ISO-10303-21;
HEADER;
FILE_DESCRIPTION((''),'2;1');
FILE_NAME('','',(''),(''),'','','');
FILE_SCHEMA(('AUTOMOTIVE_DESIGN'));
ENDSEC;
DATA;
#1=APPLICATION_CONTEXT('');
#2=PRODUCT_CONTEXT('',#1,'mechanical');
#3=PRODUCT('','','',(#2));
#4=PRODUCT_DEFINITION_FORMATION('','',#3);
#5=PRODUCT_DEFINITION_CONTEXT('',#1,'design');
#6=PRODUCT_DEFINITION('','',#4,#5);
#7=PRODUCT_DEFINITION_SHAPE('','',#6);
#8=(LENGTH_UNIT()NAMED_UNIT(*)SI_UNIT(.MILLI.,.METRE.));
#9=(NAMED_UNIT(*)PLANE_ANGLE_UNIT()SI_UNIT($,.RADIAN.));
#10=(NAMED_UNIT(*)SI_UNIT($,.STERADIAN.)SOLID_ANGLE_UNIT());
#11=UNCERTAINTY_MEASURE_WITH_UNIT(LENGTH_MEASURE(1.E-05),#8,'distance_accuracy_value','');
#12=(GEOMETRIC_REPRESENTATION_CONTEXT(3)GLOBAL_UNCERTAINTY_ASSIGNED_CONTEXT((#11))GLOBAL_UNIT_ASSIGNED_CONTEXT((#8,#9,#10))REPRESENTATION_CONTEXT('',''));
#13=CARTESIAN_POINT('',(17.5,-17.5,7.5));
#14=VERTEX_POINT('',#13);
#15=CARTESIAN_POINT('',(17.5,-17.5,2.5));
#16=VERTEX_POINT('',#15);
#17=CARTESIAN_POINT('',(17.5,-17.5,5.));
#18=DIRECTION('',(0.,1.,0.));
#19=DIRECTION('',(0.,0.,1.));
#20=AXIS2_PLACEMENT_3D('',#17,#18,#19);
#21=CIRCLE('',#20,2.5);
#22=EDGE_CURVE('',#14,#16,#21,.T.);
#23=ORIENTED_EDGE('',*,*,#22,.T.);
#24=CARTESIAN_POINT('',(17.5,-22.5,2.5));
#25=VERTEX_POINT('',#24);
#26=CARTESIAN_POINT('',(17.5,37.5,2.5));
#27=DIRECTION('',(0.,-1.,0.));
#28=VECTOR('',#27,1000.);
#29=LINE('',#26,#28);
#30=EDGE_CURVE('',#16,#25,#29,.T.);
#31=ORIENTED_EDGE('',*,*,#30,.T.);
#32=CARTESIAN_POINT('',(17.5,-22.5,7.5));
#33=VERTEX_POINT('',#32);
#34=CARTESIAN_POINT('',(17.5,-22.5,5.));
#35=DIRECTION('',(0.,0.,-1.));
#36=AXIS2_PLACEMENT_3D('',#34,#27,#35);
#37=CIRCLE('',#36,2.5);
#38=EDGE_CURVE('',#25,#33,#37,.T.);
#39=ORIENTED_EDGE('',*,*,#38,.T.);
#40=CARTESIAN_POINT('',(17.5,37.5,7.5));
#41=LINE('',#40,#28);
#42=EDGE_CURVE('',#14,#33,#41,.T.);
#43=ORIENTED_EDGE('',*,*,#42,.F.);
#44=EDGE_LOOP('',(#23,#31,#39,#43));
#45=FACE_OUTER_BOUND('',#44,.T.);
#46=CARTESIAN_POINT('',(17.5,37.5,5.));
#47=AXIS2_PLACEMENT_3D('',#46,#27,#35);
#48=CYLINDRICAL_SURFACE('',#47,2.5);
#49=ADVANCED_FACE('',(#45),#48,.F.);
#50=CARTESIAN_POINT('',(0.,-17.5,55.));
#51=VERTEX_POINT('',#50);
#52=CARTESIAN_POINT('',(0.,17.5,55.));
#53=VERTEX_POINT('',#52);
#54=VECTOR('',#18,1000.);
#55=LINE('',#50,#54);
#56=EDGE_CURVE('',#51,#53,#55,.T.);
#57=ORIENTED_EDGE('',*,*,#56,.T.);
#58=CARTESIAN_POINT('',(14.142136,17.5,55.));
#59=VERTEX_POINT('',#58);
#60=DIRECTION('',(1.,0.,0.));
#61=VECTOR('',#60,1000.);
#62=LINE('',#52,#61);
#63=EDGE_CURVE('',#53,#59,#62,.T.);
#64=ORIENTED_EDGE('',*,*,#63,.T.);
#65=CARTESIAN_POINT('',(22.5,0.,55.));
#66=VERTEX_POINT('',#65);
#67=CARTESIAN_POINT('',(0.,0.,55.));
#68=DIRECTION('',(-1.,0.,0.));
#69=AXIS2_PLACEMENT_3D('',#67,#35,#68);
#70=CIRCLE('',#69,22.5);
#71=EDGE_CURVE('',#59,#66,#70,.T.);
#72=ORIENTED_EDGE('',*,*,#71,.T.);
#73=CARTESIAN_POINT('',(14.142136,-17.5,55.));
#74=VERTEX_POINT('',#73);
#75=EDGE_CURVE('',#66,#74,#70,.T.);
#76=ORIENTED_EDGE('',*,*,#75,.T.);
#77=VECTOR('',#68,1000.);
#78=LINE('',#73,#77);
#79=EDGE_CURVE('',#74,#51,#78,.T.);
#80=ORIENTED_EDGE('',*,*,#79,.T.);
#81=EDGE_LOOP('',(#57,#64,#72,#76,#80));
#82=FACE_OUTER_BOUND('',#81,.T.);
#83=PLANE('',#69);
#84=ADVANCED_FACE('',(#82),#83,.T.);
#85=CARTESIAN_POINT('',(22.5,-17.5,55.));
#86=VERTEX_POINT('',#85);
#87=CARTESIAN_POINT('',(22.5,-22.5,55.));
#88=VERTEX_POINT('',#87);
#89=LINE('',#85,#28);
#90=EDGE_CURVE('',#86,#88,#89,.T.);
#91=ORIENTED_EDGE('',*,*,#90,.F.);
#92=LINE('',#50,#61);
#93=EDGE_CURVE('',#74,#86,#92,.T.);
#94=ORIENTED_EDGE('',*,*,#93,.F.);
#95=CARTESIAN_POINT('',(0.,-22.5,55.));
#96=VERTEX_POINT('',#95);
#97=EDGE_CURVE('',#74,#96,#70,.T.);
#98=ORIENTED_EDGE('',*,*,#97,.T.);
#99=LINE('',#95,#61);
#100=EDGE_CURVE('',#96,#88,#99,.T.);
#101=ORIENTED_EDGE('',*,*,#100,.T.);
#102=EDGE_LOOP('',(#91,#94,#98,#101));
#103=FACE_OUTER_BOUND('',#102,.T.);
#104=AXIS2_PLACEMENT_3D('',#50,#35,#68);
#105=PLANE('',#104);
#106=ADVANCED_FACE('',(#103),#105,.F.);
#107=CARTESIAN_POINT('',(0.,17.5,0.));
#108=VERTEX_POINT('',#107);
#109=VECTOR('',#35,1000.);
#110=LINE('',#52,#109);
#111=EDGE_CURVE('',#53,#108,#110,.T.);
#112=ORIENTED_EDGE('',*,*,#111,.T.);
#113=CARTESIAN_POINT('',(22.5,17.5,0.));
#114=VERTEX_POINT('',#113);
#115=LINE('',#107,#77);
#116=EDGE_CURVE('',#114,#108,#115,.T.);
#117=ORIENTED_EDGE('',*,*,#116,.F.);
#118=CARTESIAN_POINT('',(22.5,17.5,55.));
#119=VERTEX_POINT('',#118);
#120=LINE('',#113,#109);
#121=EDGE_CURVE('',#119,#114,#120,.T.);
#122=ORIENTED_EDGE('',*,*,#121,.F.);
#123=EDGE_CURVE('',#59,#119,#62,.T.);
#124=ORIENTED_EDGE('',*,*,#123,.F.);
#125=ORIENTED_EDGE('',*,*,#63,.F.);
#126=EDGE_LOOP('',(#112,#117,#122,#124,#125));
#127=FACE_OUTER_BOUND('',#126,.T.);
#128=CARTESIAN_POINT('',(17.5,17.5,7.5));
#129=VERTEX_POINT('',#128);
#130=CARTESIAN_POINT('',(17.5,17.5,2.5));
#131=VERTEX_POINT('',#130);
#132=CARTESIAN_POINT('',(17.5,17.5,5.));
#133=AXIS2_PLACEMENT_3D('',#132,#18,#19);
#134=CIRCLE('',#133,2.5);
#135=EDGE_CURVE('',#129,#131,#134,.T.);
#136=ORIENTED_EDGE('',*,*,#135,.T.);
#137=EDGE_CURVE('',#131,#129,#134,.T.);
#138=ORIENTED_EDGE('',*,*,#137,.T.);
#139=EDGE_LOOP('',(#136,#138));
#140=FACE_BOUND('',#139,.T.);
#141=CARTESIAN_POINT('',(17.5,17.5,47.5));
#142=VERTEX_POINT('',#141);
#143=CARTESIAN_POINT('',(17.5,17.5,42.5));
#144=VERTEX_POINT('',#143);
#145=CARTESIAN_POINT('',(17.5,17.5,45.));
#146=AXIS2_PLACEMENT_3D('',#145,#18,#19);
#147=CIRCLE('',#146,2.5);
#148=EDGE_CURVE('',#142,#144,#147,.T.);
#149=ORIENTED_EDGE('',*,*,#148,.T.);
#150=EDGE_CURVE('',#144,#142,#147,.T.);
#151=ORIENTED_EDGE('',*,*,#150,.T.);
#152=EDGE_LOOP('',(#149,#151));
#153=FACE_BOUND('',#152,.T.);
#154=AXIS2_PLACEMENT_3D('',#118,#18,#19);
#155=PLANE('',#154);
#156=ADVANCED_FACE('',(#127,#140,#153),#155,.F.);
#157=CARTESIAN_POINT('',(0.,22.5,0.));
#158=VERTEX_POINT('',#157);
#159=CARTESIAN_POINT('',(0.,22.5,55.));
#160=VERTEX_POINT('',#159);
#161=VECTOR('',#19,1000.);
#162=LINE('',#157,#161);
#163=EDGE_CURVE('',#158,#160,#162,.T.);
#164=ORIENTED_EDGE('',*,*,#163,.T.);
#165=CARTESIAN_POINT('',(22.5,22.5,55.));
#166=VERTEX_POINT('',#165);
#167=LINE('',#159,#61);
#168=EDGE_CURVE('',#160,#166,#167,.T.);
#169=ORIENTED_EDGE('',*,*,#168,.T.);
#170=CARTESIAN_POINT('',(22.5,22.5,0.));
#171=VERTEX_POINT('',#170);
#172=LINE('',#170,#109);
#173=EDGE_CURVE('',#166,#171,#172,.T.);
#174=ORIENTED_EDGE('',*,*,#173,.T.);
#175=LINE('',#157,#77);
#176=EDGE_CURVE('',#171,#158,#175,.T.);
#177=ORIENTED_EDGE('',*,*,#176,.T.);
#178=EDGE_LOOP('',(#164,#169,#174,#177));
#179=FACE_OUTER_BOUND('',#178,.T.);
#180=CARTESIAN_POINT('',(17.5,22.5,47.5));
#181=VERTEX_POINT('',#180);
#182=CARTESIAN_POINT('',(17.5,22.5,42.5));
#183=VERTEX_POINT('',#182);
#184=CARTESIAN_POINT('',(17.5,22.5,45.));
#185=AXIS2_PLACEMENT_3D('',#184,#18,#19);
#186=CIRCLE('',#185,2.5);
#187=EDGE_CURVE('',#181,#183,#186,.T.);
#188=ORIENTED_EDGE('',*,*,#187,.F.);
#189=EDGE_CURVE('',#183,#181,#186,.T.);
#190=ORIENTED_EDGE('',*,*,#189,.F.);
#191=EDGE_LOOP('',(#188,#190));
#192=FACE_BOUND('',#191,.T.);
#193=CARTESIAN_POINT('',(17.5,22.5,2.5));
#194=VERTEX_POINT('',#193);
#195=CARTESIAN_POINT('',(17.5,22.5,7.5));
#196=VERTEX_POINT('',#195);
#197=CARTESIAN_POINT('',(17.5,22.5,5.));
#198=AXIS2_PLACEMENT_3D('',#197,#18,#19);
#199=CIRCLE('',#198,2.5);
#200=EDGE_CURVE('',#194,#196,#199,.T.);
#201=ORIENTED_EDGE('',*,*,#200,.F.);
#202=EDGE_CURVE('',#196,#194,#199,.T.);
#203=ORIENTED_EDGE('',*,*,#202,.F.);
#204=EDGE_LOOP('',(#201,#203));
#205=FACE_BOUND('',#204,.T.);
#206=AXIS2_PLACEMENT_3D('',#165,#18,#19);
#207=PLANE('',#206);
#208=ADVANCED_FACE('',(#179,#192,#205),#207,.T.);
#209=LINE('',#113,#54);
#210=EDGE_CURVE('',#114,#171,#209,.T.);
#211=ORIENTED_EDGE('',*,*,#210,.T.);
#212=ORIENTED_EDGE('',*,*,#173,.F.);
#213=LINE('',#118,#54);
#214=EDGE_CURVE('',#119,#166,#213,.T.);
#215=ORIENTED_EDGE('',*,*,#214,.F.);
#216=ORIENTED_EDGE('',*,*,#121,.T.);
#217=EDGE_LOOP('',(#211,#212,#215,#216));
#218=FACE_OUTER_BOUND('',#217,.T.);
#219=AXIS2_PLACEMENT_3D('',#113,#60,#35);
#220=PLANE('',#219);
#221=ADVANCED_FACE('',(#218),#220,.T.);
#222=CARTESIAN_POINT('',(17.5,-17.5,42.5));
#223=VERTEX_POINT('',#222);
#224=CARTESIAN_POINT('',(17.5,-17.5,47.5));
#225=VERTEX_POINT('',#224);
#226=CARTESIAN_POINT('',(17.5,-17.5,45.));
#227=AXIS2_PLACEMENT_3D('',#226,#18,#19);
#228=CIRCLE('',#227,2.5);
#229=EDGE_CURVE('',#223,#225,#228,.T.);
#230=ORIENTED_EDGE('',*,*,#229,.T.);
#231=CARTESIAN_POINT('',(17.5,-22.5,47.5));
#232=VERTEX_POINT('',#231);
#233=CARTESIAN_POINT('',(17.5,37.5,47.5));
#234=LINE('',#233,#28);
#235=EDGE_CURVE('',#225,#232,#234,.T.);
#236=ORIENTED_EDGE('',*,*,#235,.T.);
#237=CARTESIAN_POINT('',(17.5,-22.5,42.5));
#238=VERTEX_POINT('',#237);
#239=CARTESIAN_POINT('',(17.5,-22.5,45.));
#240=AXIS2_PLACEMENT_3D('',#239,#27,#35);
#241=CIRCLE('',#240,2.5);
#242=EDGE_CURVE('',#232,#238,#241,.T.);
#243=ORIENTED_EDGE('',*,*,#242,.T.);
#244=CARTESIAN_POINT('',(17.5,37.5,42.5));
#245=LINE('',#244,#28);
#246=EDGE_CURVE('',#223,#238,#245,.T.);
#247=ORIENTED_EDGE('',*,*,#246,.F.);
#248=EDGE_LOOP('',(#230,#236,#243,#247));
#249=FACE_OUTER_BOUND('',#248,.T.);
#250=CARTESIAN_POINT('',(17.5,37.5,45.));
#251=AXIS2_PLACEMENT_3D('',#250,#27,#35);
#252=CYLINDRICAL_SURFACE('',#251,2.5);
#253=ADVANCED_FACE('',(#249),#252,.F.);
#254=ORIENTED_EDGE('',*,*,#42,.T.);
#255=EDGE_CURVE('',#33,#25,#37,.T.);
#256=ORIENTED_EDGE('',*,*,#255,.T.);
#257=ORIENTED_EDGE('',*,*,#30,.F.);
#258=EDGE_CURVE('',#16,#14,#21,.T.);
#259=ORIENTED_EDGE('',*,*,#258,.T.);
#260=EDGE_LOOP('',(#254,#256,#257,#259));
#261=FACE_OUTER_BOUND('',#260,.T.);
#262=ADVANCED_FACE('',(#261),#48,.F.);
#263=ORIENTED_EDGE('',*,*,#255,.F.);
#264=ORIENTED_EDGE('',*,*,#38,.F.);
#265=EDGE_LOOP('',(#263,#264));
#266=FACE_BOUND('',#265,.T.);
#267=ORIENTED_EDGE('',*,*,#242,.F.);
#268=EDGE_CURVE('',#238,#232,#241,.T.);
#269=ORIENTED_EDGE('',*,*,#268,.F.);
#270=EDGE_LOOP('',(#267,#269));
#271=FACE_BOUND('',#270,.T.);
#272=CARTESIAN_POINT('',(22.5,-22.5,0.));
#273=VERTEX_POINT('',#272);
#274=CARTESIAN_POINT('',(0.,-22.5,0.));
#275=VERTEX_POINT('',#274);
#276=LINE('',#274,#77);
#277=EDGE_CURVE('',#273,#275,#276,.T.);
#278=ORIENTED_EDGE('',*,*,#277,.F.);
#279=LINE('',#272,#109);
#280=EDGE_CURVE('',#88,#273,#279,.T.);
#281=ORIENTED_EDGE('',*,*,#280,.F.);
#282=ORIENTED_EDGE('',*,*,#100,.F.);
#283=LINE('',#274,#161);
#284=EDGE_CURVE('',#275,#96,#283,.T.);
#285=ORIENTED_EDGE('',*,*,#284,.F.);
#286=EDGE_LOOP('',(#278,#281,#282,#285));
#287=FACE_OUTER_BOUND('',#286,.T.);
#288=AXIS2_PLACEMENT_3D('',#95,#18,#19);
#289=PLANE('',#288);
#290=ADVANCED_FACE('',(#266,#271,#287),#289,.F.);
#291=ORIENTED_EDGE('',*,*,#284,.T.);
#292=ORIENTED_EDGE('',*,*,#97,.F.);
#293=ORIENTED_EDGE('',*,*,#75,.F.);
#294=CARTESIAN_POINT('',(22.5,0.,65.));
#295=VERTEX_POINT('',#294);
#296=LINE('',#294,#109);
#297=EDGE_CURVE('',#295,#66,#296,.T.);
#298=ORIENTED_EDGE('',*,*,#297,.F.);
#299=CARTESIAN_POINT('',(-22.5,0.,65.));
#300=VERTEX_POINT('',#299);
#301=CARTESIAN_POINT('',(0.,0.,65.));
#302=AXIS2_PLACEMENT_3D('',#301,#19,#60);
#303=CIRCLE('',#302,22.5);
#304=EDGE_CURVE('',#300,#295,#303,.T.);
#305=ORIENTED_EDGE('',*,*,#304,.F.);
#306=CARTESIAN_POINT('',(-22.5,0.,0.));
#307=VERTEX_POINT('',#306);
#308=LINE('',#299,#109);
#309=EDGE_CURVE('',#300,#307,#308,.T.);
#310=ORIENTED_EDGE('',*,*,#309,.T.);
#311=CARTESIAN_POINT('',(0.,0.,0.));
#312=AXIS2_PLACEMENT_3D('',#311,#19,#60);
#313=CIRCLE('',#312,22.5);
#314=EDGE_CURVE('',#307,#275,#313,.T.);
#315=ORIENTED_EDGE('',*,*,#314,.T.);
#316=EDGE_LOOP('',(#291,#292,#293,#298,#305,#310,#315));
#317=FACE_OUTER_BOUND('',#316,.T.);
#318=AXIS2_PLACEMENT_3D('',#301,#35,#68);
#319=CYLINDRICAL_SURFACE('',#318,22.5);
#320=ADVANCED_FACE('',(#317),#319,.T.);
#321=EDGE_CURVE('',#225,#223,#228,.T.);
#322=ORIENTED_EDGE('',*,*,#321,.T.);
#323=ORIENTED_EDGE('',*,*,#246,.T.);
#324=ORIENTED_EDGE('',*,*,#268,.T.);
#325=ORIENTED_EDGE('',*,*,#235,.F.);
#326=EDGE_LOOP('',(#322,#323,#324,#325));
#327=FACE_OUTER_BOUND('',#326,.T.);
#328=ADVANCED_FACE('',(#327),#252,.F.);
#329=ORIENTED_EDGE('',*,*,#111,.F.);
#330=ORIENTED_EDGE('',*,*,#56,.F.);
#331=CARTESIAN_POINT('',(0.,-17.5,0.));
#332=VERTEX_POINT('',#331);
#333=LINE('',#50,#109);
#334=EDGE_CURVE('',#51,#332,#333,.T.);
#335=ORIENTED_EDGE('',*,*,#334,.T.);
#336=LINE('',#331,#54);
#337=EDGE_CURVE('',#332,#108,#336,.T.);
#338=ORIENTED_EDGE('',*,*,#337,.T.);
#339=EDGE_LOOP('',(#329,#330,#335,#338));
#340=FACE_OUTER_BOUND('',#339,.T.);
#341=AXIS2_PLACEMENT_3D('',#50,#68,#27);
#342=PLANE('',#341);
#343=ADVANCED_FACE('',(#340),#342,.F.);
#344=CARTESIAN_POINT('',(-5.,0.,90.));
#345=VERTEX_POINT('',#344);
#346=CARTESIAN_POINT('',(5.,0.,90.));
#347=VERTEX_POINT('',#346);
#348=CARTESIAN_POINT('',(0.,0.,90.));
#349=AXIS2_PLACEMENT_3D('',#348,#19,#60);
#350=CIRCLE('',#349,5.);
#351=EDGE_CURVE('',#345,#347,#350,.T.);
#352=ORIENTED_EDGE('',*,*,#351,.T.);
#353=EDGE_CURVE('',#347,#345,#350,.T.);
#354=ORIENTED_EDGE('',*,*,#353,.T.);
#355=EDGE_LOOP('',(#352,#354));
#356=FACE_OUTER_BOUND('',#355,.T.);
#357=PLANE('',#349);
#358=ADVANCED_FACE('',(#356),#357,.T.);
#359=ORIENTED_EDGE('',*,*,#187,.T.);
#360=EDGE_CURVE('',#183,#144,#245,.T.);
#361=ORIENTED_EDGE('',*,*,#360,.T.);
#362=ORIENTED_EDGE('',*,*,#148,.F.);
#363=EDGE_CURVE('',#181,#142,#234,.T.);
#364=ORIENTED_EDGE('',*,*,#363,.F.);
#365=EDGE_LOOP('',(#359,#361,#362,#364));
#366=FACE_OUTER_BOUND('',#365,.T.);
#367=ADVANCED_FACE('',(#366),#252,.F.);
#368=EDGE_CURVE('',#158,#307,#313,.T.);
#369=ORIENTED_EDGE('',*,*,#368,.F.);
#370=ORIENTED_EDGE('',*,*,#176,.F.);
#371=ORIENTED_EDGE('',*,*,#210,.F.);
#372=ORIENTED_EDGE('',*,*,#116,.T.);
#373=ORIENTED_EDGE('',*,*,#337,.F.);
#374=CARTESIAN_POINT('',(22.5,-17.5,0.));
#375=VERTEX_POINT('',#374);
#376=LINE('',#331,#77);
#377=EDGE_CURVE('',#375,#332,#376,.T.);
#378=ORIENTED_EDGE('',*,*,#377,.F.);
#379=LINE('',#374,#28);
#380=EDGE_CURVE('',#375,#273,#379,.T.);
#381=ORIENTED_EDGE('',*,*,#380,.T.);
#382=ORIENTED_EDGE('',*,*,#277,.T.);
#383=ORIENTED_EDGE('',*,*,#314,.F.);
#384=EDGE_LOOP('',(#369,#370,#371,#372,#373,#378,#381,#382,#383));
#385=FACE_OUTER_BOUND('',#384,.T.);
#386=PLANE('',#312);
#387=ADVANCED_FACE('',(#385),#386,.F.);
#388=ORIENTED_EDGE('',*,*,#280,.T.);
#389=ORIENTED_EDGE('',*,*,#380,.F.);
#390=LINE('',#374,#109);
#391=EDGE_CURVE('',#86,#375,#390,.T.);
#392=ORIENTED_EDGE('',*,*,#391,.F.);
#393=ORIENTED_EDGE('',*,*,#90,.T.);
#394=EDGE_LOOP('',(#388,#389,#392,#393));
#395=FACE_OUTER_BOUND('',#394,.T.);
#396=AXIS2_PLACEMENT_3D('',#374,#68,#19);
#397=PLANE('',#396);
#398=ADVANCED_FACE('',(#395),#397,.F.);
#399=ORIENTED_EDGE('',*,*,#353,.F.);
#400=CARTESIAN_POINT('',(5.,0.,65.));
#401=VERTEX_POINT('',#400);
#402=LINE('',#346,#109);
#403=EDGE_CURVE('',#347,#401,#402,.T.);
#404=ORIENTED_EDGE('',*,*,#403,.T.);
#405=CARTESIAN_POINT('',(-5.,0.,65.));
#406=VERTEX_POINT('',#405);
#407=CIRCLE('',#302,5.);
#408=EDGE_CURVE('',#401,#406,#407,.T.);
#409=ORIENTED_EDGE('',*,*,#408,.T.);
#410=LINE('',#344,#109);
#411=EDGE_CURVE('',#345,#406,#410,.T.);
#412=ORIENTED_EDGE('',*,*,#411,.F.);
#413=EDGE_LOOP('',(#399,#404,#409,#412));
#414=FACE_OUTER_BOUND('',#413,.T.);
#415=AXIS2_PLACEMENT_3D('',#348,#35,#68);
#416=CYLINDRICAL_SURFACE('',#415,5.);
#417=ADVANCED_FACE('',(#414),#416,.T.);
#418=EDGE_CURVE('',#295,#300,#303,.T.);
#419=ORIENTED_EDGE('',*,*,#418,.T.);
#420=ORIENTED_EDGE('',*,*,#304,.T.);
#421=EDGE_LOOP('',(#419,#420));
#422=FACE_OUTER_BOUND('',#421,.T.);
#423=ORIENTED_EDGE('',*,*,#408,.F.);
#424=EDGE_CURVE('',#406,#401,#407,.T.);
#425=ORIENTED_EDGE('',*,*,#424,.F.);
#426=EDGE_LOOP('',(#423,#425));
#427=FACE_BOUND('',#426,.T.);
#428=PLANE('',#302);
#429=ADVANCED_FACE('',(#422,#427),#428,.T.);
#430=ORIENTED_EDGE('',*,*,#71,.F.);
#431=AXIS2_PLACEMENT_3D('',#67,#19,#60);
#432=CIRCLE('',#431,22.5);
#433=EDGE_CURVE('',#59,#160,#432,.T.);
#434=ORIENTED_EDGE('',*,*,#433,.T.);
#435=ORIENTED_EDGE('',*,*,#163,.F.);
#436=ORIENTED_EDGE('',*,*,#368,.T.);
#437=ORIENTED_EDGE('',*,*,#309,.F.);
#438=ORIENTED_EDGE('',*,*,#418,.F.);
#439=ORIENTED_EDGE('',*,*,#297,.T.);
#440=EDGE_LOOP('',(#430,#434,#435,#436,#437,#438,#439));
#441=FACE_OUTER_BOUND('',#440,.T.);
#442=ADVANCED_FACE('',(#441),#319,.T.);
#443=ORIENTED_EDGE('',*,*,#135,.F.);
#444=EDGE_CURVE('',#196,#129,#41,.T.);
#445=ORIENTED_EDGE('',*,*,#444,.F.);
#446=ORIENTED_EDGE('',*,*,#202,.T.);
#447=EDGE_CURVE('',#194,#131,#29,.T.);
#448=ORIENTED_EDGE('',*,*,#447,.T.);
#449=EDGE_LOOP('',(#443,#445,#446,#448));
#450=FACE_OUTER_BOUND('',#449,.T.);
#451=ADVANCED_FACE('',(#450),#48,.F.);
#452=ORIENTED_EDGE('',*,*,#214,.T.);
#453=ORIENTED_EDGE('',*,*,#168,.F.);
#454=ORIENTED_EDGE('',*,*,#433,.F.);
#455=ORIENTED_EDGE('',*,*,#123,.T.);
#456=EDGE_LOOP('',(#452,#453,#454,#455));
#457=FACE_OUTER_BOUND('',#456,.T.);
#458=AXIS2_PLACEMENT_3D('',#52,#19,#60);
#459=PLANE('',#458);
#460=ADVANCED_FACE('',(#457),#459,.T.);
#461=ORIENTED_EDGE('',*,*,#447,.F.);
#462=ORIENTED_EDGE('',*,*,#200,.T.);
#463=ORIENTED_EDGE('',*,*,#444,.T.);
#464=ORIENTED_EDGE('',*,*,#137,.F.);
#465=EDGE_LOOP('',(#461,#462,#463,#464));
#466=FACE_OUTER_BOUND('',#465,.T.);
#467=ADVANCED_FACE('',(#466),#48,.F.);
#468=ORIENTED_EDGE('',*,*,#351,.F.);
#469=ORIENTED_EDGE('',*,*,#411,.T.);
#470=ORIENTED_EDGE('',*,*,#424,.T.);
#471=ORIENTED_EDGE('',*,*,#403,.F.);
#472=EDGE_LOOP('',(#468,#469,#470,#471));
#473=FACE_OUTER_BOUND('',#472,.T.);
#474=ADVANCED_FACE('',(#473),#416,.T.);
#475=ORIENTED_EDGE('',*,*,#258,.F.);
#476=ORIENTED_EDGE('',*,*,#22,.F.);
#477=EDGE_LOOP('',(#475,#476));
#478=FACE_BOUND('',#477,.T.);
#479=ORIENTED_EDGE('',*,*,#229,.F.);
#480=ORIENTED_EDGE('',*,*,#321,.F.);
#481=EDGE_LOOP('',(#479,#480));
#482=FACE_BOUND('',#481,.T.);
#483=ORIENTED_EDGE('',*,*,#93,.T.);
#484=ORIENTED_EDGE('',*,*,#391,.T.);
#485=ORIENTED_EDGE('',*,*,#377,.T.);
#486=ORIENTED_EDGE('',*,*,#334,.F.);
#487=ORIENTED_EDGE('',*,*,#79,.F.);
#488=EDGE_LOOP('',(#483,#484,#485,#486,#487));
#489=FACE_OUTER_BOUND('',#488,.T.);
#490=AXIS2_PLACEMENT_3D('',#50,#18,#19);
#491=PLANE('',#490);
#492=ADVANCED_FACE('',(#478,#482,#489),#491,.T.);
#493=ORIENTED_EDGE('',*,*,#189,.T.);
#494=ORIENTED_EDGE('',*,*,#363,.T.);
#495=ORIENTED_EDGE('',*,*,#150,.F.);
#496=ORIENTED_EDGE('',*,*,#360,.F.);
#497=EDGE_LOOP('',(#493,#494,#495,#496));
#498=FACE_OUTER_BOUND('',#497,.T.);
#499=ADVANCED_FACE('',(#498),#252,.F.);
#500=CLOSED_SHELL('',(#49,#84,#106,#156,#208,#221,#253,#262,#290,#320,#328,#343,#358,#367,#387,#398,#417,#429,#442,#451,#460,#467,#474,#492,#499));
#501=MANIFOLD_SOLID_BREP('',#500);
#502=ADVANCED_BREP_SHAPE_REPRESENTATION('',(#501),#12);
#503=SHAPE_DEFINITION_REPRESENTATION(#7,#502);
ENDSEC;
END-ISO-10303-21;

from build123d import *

# Parameters (mm, degrees)
SKETCH_1_R          = 22.5
EXTRUDE_1_DEPTH     = 65
SKETCH_2_R          = 5
EXTRUDE_2_DEPTH     = 25
SKETCH_3_W          = 22.5
SKETCH_3_H          = 55
EXTRUDE_3_DEPTH     = 5
SKETCH_4_W          = 22.5
SKETCH_4_H          = 55
EXTRUDE_4_DEPTH     = 5
CUT_EXTRUDE_1_DEPTH = 55
SKETCH_6_R          = 2.5
CUT_EXTRUDE_2_DEPTH = 60


with BuildPart() as part:
    # 草图1 → 凸台-拉伸1 (new body)
    with BuildSketch(Plane.XY):
        Circle(SKETCH_1_R)
    extrude(amount=EXTRUDE_1_DEPTH)

    # 草图2 → 凸台-拉伸2 (add)
    with BuildSketch(Plane.XY.offset(65)):
        Circle(SKETCH_2_R)
    extrude(amount=EXTRUDE_2_DEPTH)

    # 草图3 → 凸台-拉伸3 (add)
    with BuildSketch(Plane(origin=(0, 22.5, 0), x_dir=(-1, 0, 0), z_dir=(0, 1, 0))):
        with Locations((-11.25, 27.5)):
            Rectangle(SKETCH_3_W, SKETCH_3_H)
    extrude(amount=-EXTRUDE_3_DEPTH)

    # 草图4 → 凸台-拉伸4 (add)
    with BuildSketch(Plane(origin=(0, -22.5, 0), x_dir=(-1, 0, 0), z_dir=(0, 1, 0))):
        with Locations((-11.25, 27.5)):
            Rectangle(SKETCH_4_W, SKETCH_4_H)
    extrude(amount=EXTRUDE_4_DEPTH)

    # 草图5 → 切除-拉伸1 (cut)
    with BuildSketch(Plane(origin=(0, 0, 0), x_dir=(-1, 0, 0), z_dir=(0, 0, -1))):
        with BuildLine():
            Line((-14.142135624, -17.5), (0, -17.5))
            Line((0, -17.5), (0, 17.5))
            Line((0, 17.5), (-14.142135624, 17.5))
            ThreePointArc((-14.142135624, 17.5), (-22.5, 0), (-14.142135624, -17.5))
        make_face()
    extrude(amount=-CUT_EXTRUDE_1_DEPTH, mode=Mode.SUBTRACT)

    # 草图6 → 切除-拉伸2 (cut)
    with BuildSketch(Plane.XZ.offset(22.5)):
        with Locations(Location((17.5, 5, 0), (0, 0, 270))):
            Circle(SKETCH_6_R)
        with Locations(Location((17.5, 45, 0), (0, 0, 270))):
            Circle(SKETCH_6_R)
    extrude(amount=-CUT_EXTRUDE_2_DEPTH, mode=Mode.SUBTRACT)


solid = part.part
